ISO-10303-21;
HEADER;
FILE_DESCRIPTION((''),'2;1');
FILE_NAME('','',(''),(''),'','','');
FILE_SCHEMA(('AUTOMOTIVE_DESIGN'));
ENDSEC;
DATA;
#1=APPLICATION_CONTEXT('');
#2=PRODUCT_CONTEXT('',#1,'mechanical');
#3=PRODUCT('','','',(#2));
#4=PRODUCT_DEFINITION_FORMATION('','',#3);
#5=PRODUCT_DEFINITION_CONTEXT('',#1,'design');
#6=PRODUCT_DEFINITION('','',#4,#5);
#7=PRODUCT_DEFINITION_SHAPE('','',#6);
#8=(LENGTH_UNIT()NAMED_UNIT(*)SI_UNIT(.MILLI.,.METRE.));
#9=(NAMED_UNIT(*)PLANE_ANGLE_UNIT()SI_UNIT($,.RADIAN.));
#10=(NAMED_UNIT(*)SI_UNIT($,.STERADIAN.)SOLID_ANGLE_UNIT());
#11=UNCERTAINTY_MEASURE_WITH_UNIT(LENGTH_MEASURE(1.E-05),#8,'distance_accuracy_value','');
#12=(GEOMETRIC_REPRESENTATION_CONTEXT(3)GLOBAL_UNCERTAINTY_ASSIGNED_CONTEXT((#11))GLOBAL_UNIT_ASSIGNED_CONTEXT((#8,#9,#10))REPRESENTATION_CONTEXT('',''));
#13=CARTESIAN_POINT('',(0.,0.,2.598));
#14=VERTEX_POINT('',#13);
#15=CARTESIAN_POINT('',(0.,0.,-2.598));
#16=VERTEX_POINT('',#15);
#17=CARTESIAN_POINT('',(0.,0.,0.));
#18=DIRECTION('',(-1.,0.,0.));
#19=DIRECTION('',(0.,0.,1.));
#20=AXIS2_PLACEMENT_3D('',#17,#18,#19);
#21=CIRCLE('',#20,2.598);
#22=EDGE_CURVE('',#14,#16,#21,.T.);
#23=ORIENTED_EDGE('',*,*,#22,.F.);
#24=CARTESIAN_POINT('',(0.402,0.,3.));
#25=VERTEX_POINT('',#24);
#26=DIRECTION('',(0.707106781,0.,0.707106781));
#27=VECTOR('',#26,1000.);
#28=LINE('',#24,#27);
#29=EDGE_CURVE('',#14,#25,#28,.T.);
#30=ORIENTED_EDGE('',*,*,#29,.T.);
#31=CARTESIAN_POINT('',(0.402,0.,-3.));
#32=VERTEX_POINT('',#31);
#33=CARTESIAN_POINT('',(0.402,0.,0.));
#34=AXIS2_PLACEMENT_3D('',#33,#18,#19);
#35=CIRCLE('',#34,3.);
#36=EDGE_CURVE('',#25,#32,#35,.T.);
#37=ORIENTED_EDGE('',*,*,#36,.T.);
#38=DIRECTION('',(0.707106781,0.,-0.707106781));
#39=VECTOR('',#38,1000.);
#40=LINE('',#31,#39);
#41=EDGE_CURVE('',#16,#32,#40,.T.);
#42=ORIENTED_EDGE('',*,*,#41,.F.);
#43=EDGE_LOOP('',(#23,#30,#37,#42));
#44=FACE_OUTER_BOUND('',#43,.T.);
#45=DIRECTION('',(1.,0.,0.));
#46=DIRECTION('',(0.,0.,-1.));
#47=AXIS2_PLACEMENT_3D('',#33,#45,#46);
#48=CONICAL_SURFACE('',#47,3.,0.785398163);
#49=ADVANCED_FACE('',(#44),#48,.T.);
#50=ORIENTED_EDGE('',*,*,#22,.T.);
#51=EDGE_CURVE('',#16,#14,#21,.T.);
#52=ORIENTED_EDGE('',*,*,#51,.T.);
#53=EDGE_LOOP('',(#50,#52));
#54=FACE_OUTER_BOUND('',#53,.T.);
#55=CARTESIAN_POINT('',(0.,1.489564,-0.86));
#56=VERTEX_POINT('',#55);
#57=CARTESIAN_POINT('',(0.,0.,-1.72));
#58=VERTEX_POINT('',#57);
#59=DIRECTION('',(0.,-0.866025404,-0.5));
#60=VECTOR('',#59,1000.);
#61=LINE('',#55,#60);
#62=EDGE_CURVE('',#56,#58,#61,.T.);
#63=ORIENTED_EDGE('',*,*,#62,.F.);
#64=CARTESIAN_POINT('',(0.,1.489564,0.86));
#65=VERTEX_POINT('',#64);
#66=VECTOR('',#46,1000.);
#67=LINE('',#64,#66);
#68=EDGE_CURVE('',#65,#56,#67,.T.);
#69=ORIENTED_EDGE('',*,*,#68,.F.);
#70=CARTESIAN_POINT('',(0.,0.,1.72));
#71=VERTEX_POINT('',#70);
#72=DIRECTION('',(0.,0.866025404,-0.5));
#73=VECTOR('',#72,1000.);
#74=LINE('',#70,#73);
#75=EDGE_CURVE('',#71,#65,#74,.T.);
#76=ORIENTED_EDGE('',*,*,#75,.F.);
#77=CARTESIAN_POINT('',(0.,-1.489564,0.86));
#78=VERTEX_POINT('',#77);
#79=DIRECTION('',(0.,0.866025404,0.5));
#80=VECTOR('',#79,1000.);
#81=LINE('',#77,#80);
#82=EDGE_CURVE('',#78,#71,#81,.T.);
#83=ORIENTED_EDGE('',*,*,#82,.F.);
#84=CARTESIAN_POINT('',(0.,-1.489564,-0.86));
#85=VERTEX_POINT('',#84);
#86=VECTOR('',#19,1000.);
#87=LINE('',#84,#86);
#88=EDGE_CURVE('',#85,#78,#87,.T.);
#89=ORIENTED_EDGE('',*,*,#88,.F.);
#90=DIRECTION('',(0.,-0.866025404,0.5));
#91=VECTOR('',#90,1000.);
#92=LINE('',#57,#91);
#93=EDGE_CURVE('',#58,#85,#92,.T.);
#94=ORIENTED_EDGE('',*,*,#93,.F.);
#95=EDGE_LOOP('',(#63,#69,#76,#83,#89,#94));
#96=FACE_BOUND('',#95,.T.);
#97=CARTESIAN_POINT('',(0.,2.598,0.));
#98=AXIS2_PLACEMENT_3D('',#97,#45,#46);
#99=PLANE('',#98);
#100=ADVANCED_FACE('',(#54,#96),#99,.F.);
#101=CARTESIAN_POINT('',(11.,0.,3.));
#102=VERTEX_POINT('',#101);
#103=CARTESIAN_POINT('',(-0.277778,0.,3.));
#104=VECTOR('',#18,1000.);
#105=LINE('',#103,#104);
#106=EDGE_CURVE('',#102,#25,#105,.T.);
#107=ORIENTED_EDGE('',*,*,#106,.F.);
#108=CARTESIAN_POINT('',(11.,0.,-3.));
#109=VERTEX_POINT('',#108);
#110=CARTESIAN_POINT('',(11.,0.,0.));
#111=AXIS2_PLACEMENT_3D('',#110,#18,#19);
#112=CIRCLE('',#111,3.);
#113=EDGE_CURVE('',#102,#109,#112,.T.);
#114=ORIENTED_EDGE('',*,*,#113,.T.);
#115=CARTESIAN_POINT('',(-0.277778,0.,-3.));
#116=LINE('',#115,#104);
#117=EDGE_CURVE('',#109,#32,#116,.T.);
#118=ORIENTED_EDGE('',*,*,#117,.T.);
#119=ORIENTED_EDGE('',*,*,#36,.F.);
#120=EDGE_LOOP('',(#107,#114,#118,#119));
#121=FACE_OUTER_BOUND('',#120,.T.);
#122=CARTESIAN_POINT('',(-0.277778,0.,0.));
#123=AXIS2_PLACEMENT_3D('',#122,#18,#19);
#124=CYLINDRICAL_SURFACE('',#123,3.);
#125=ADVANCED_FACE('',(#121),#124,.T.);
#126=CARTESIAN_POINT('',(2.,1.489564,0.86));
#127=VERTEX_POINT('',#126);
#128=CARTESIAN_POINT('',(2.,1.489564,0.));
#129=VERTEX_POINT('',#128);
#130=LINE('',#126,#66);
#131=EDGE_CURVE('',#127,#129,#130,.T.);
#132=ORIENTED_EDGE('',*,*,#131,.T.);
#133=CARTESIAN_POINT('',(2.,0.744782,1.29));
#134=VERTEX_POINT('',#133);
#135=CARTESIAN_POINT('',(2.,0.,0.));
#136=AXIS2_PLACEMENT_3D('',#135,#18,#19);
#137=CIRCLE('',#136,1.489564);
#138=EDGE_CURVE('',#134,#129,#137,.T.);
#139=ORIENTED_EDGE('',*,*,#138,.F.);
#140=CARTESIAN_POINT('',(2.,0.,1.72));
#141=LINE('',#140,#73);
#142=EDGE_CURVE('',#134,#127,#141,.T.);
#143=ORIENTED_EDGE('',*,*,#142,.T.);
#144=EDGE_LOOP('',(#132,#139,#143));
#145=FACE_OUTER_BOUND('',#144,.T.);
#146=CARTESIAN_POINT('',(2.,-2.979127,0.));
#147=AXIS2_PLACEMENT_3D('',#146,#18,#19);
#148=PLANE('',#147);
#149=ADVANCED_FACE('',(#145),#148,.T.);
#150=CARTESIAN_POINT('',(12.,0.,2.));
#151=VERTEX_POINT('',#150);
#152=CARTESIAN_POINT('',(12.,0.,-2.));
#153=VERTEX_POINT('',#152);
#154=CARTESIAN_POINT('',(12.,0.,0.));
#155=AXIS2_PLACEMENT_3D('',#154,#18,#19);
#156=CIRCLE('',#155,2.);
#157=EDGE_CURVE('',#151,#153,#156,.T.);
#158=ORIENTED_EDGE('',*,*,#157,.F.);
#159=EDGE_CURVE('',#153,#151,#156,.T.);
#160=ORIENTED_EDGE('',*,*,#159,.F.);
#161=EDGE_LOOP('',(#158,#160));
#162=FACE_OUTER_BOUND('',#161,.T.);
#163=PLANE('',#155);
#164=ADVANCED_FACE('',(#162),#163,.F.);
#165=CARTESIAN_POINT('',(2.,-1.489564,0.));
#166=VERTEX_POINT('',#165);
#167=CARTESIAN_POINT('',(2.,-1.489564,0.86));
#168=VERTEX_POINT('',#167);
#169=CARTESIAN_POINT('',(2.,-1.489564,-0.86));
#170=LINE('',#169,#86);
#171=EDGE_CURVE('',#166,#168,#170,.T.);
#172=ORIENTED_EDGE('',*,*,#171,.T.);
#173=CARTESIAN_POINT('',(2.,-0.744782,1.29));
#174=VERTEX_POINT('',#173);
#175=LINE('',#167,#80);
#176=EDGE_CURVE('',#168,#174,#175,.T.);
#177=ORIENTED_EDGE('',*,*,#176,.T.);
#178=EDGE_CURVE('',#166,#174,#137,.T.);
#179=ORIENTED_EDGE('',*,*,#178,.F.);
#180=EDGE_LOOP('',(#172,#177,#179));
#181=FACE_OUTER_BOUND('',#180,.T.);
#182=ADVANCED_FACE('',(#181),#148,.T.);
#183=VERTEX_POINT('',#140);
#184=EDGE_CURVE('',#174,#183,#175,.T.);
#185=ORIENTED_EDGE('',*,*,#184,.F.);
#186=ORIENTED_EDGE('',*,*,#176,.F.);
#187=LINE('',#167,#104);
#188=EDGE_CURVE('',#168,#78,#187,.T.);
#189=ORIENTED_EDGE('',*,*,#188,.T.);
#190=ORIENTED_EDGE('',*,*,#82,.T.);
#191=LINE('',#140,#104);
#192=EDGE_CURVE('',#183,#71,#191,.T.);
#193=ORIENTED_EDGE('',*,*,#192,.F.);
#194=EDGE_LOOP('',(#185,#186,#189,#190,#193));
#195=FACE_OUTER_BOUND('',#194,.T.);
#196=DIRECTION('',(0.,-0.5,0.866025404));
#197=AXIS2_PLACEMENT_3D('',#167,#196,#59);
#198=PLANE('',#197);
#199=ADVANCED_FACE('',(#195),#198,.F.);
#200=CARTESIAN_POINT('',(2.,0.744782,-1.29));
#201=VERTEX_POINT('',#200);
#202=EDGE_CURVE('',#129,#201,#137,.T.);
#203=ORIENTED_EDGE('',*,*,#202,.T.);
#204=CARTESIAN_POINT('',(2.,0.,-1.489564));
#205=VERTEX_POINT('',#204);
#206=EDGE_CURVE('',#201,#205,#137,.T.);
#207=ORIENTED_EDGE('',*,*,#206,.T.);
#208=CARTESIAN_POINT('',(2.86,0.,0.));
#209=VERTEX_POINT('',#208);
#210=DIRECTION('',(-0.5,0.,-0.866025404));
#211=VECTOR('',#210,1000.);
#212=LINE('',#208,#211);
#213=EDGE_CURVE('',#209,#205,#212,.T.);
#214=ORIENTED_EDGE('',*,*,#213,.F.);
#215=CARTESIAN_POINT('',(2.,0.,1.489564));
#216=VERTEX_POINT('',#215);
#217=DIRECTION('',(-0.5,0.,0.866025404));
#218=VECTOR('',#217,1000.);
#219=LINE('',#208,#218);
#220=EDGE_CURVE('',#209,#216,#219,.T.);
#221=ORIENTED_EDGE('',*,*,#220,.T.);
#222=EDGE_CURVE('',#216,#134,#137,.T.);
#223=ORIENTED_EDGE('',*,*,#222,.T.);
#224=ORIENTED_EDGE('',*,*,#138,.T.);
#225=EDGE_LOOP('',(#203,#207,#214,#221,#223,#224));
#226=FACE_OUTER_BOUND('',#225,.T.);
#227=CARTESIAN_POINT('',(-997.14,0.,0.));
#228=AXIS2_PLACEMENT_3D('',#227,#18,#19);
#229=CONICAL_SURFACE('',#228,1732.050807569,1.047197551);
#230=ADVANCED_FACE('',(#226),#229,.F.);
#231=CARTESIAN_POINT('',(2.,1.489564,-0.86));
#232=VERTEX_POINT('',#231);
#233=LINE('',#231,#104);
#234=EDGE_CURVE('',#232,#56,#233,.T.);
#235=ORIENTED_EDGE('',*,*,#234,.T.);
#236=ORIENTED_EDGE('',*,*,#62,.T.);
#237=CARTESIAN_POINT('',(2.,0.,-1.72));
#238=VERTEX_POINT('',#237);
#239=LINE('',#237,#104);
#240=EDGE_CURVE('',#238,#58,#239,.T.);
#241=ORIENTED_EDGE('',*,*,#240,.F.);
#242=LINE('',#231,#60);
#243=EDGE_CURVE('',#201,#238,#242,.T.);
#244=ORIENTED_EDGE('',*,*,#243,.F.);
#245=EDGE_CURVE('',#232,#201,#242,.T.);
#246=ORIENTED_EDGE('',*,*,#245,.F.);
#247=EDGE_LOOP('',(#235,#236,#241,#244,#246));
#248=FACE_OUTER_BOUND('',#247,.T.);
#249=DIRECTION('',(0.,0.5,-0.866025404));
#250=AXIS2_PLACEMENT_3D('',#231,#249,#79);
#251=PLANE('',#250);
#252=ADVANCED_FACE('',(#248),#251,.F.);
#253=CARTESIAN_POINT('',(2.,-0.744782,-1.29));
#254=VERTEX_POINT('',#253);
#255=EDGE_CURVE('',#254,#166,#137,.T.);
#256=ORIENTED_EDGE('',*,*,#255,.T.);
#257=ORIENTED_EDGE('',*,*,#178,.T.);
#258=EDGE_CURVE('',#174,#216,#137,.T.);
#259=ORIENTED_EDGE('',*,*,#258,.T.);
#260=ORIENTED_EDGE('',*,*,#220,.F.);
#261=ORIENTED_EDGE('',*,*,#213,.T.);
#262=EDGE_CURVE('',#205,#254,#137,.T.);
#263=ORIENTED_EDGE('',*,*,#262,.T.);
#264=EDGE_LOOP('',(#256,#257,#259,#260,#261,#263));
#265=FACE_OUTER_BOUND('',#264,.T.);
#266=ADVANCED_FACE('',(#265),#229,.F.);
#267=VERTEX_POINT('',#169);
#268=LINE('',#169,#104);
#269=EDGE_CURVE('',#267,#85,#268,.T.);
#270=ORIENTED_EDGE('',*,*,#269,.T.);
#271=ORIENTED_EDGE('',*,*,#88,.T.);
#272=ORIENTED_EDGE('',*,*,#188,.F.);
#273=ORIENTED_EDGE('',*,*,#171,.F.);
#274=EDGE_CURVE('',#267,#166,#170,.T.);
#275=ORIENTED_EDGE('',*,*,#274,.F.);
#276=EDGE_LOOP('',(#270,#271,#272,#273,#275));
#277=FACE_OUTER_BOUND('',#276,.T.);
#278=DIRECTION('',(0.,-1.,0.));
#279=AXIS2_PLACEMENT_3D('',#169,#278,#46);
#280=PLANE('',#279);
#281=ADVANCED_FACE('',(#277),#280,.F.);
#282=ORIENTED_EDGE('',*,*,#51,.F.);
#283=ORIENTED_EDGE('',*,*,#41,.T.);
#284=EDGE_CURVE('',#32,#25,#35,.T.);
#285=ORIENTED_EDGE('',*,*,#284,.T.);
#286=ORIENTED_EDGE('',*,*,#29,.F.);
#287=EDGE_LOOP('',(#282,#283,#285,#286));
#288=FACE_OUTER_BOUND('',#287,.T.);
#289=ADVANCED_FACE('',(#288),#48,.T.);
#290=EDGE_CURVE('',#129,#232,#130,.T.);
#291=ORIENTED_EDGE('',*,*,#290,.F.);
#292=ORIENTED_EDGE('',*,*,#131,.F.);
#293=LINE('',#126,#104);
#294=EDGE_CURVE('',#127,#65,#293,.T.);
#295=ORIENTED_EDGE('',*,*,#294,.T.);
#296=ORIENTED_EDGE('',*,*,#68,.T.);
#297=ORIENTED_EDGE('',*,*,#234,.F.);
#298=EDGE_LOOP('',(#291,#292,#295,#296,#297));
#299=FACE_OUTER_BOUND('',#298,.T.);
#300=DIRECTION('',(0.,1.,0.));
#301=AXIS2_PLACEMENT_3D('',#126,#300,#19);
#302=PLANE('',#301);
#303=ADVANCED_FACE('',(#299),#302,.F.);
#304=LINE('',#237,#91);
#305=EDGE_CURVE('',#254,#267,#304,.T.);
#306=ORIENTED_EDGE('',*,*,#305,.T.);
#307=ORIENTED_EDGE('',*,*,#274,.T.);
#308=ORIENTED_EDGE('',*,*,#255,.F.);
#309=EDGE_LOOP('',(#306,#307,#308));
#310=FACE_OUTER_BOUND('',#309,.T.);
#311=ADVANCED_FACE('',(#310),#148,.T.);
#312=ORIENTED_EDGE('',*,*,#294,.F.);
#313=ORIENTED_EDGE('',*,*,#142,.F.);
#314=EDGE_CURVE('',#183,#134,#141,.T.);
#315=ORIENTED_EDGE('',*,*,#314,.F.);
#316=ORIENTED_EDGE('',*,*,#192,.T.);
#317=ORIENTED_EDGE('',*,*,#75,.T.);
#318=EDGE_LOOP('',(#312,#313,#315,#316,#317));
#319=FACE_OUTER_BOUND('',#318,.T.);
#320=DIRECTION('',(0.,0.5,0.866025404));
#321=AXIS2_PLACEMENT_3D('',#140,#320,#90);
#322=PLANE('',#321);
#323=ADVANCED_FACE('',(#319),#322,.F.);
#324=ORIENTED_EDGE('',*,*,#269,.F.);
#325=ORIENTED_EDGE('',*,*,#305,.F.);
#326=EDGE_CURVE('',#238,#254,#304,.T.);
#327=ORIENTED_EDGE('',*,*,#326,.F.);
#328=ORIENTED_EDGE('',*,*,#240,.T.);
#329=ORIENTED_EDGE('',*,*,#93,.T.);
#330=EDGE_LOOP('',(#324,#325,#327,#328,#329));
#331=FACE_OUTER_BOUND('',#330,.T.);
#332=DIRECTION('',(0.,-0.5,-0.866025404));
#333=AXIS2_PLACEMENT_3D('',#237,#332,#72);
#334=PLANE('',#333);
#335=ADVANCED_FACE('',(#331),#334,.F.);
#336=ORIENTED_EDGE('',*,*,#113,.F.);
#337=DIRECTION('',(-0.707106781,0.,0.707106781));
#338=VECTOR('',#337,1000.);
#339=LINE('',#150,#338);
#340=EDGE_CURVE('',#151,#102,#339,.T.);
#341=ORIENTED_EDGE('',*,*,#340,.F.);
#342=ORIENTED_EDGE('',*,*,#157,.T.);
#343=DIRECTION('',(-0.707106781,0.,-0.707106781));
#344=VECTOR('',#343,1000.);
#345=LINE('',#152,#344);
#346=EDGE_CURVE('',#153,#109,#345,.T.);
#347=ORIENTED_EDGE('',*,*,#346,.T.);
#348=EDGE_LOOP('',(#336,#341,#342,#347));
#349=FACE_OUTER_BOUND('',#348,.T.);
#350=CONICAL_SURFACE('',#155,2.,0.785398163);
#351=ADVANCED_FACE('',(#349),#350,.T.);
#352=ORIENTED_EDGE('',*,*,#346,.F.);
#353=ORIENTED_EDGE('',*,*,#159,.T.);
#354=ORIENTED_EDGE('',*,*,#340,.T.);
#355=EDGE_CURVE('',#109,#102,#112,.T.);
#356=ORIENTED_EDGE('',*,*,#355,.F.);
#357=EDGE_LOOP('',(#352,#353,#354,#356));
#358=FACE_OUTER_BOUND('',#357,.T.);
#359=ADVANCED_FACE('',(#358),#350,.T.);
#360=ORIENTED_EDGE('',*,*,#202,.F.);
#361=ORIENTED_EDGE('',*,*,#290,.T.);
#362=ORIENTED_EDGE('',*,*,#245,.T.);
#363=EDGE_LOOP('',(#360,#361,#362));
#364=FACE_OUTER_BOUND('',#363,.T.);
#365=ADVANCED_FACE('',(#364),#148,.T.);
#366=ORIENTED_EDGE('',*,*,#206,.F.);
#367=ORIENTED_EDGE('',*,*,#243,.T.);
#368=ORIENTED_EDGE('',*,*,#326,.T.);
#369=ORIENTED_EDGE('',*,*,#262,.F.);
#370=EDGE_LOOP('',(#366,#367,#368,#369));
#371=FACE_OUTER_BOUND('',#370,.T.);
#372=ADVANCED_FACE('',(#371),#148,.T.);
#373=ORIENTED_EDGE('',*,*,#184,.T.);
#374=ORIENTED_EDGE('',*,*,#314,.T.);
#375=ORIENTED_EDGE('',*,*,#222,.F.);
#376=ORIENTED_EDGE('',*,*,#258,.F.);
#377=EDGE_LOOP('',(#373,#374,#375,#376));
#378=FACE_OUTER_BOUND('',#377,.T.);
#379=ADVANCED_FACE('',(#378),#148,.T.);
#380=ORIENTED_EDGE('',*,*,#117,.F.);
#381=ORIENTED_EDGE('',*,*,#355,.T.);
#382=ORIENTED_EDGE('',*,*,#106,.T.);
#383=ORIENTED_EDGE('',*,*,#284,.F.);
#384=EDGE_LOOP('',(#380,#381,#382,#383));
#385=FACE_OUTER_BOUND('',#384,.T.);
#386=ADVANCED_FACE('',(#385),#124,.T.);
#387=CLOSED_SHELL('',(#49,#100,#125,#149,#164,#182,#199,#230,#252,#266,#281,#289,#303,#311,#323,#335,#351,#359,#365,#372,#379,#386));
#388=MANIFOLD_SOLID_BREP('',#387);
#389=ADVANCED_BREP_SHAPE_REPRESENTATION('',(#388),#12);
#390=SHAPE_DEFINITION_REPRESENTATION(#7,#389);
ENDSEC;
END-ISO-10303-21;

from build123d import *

# Parameters (mm, degrees)
CUT_EXTRUDE1_DEPTH = 2


with BuildPart() as part:
    # Sketch1 → Base-Revolve (revolve)
    with BuildSketch(Plane.XY, mode=Mode.PRIVATE) as base_revolve_sk:
        Polygon((0, 0), (12, 0), (12, 2), (11, 3), (0.402, 3), (0, 2.598), align=None)
    revolve(base_revolve_sk.sketch.rotate(Axis((-0.277777778, 0, 0), (1, 0, 0)), 90), axis=Axis((-0.277777778, 0, 0), (1, 0, 0)))

    # Sketch2 → Cut-Extrude1 (cut)
    with BuildSketch(Plane.ZY):
        Polygon((-0.86, -1.489563695), (0.86, -1.489563695), (1.72, 0), (0.86, 1.489563695), (-0.86, 1.489563695), (-1.72, 0), align=None)
    extrude(amount=-CUT_EXTRUDE1_DEPTH, mode=Mode.SUBTRACT)

    # Sketch4 → Cut-Revolve2 (revolve, cut)
    with BuildSketch(Plane.XY, mode=Mode.PRIVATE) as cut_revolve2_sk:
        Polygon((2, 1.489563695), (2.86, 0), (2, 0), align=None)
    revolve(cut_revolve2_sk.sketch.rotate(Axis((-0.277777778, 0, 0), (1, 0, 0)), 90), axis=Axis((-0.277777778, 0, 0), (1, 0, 0)), mode=Mode.SUBTRACT)


solid = part.part
